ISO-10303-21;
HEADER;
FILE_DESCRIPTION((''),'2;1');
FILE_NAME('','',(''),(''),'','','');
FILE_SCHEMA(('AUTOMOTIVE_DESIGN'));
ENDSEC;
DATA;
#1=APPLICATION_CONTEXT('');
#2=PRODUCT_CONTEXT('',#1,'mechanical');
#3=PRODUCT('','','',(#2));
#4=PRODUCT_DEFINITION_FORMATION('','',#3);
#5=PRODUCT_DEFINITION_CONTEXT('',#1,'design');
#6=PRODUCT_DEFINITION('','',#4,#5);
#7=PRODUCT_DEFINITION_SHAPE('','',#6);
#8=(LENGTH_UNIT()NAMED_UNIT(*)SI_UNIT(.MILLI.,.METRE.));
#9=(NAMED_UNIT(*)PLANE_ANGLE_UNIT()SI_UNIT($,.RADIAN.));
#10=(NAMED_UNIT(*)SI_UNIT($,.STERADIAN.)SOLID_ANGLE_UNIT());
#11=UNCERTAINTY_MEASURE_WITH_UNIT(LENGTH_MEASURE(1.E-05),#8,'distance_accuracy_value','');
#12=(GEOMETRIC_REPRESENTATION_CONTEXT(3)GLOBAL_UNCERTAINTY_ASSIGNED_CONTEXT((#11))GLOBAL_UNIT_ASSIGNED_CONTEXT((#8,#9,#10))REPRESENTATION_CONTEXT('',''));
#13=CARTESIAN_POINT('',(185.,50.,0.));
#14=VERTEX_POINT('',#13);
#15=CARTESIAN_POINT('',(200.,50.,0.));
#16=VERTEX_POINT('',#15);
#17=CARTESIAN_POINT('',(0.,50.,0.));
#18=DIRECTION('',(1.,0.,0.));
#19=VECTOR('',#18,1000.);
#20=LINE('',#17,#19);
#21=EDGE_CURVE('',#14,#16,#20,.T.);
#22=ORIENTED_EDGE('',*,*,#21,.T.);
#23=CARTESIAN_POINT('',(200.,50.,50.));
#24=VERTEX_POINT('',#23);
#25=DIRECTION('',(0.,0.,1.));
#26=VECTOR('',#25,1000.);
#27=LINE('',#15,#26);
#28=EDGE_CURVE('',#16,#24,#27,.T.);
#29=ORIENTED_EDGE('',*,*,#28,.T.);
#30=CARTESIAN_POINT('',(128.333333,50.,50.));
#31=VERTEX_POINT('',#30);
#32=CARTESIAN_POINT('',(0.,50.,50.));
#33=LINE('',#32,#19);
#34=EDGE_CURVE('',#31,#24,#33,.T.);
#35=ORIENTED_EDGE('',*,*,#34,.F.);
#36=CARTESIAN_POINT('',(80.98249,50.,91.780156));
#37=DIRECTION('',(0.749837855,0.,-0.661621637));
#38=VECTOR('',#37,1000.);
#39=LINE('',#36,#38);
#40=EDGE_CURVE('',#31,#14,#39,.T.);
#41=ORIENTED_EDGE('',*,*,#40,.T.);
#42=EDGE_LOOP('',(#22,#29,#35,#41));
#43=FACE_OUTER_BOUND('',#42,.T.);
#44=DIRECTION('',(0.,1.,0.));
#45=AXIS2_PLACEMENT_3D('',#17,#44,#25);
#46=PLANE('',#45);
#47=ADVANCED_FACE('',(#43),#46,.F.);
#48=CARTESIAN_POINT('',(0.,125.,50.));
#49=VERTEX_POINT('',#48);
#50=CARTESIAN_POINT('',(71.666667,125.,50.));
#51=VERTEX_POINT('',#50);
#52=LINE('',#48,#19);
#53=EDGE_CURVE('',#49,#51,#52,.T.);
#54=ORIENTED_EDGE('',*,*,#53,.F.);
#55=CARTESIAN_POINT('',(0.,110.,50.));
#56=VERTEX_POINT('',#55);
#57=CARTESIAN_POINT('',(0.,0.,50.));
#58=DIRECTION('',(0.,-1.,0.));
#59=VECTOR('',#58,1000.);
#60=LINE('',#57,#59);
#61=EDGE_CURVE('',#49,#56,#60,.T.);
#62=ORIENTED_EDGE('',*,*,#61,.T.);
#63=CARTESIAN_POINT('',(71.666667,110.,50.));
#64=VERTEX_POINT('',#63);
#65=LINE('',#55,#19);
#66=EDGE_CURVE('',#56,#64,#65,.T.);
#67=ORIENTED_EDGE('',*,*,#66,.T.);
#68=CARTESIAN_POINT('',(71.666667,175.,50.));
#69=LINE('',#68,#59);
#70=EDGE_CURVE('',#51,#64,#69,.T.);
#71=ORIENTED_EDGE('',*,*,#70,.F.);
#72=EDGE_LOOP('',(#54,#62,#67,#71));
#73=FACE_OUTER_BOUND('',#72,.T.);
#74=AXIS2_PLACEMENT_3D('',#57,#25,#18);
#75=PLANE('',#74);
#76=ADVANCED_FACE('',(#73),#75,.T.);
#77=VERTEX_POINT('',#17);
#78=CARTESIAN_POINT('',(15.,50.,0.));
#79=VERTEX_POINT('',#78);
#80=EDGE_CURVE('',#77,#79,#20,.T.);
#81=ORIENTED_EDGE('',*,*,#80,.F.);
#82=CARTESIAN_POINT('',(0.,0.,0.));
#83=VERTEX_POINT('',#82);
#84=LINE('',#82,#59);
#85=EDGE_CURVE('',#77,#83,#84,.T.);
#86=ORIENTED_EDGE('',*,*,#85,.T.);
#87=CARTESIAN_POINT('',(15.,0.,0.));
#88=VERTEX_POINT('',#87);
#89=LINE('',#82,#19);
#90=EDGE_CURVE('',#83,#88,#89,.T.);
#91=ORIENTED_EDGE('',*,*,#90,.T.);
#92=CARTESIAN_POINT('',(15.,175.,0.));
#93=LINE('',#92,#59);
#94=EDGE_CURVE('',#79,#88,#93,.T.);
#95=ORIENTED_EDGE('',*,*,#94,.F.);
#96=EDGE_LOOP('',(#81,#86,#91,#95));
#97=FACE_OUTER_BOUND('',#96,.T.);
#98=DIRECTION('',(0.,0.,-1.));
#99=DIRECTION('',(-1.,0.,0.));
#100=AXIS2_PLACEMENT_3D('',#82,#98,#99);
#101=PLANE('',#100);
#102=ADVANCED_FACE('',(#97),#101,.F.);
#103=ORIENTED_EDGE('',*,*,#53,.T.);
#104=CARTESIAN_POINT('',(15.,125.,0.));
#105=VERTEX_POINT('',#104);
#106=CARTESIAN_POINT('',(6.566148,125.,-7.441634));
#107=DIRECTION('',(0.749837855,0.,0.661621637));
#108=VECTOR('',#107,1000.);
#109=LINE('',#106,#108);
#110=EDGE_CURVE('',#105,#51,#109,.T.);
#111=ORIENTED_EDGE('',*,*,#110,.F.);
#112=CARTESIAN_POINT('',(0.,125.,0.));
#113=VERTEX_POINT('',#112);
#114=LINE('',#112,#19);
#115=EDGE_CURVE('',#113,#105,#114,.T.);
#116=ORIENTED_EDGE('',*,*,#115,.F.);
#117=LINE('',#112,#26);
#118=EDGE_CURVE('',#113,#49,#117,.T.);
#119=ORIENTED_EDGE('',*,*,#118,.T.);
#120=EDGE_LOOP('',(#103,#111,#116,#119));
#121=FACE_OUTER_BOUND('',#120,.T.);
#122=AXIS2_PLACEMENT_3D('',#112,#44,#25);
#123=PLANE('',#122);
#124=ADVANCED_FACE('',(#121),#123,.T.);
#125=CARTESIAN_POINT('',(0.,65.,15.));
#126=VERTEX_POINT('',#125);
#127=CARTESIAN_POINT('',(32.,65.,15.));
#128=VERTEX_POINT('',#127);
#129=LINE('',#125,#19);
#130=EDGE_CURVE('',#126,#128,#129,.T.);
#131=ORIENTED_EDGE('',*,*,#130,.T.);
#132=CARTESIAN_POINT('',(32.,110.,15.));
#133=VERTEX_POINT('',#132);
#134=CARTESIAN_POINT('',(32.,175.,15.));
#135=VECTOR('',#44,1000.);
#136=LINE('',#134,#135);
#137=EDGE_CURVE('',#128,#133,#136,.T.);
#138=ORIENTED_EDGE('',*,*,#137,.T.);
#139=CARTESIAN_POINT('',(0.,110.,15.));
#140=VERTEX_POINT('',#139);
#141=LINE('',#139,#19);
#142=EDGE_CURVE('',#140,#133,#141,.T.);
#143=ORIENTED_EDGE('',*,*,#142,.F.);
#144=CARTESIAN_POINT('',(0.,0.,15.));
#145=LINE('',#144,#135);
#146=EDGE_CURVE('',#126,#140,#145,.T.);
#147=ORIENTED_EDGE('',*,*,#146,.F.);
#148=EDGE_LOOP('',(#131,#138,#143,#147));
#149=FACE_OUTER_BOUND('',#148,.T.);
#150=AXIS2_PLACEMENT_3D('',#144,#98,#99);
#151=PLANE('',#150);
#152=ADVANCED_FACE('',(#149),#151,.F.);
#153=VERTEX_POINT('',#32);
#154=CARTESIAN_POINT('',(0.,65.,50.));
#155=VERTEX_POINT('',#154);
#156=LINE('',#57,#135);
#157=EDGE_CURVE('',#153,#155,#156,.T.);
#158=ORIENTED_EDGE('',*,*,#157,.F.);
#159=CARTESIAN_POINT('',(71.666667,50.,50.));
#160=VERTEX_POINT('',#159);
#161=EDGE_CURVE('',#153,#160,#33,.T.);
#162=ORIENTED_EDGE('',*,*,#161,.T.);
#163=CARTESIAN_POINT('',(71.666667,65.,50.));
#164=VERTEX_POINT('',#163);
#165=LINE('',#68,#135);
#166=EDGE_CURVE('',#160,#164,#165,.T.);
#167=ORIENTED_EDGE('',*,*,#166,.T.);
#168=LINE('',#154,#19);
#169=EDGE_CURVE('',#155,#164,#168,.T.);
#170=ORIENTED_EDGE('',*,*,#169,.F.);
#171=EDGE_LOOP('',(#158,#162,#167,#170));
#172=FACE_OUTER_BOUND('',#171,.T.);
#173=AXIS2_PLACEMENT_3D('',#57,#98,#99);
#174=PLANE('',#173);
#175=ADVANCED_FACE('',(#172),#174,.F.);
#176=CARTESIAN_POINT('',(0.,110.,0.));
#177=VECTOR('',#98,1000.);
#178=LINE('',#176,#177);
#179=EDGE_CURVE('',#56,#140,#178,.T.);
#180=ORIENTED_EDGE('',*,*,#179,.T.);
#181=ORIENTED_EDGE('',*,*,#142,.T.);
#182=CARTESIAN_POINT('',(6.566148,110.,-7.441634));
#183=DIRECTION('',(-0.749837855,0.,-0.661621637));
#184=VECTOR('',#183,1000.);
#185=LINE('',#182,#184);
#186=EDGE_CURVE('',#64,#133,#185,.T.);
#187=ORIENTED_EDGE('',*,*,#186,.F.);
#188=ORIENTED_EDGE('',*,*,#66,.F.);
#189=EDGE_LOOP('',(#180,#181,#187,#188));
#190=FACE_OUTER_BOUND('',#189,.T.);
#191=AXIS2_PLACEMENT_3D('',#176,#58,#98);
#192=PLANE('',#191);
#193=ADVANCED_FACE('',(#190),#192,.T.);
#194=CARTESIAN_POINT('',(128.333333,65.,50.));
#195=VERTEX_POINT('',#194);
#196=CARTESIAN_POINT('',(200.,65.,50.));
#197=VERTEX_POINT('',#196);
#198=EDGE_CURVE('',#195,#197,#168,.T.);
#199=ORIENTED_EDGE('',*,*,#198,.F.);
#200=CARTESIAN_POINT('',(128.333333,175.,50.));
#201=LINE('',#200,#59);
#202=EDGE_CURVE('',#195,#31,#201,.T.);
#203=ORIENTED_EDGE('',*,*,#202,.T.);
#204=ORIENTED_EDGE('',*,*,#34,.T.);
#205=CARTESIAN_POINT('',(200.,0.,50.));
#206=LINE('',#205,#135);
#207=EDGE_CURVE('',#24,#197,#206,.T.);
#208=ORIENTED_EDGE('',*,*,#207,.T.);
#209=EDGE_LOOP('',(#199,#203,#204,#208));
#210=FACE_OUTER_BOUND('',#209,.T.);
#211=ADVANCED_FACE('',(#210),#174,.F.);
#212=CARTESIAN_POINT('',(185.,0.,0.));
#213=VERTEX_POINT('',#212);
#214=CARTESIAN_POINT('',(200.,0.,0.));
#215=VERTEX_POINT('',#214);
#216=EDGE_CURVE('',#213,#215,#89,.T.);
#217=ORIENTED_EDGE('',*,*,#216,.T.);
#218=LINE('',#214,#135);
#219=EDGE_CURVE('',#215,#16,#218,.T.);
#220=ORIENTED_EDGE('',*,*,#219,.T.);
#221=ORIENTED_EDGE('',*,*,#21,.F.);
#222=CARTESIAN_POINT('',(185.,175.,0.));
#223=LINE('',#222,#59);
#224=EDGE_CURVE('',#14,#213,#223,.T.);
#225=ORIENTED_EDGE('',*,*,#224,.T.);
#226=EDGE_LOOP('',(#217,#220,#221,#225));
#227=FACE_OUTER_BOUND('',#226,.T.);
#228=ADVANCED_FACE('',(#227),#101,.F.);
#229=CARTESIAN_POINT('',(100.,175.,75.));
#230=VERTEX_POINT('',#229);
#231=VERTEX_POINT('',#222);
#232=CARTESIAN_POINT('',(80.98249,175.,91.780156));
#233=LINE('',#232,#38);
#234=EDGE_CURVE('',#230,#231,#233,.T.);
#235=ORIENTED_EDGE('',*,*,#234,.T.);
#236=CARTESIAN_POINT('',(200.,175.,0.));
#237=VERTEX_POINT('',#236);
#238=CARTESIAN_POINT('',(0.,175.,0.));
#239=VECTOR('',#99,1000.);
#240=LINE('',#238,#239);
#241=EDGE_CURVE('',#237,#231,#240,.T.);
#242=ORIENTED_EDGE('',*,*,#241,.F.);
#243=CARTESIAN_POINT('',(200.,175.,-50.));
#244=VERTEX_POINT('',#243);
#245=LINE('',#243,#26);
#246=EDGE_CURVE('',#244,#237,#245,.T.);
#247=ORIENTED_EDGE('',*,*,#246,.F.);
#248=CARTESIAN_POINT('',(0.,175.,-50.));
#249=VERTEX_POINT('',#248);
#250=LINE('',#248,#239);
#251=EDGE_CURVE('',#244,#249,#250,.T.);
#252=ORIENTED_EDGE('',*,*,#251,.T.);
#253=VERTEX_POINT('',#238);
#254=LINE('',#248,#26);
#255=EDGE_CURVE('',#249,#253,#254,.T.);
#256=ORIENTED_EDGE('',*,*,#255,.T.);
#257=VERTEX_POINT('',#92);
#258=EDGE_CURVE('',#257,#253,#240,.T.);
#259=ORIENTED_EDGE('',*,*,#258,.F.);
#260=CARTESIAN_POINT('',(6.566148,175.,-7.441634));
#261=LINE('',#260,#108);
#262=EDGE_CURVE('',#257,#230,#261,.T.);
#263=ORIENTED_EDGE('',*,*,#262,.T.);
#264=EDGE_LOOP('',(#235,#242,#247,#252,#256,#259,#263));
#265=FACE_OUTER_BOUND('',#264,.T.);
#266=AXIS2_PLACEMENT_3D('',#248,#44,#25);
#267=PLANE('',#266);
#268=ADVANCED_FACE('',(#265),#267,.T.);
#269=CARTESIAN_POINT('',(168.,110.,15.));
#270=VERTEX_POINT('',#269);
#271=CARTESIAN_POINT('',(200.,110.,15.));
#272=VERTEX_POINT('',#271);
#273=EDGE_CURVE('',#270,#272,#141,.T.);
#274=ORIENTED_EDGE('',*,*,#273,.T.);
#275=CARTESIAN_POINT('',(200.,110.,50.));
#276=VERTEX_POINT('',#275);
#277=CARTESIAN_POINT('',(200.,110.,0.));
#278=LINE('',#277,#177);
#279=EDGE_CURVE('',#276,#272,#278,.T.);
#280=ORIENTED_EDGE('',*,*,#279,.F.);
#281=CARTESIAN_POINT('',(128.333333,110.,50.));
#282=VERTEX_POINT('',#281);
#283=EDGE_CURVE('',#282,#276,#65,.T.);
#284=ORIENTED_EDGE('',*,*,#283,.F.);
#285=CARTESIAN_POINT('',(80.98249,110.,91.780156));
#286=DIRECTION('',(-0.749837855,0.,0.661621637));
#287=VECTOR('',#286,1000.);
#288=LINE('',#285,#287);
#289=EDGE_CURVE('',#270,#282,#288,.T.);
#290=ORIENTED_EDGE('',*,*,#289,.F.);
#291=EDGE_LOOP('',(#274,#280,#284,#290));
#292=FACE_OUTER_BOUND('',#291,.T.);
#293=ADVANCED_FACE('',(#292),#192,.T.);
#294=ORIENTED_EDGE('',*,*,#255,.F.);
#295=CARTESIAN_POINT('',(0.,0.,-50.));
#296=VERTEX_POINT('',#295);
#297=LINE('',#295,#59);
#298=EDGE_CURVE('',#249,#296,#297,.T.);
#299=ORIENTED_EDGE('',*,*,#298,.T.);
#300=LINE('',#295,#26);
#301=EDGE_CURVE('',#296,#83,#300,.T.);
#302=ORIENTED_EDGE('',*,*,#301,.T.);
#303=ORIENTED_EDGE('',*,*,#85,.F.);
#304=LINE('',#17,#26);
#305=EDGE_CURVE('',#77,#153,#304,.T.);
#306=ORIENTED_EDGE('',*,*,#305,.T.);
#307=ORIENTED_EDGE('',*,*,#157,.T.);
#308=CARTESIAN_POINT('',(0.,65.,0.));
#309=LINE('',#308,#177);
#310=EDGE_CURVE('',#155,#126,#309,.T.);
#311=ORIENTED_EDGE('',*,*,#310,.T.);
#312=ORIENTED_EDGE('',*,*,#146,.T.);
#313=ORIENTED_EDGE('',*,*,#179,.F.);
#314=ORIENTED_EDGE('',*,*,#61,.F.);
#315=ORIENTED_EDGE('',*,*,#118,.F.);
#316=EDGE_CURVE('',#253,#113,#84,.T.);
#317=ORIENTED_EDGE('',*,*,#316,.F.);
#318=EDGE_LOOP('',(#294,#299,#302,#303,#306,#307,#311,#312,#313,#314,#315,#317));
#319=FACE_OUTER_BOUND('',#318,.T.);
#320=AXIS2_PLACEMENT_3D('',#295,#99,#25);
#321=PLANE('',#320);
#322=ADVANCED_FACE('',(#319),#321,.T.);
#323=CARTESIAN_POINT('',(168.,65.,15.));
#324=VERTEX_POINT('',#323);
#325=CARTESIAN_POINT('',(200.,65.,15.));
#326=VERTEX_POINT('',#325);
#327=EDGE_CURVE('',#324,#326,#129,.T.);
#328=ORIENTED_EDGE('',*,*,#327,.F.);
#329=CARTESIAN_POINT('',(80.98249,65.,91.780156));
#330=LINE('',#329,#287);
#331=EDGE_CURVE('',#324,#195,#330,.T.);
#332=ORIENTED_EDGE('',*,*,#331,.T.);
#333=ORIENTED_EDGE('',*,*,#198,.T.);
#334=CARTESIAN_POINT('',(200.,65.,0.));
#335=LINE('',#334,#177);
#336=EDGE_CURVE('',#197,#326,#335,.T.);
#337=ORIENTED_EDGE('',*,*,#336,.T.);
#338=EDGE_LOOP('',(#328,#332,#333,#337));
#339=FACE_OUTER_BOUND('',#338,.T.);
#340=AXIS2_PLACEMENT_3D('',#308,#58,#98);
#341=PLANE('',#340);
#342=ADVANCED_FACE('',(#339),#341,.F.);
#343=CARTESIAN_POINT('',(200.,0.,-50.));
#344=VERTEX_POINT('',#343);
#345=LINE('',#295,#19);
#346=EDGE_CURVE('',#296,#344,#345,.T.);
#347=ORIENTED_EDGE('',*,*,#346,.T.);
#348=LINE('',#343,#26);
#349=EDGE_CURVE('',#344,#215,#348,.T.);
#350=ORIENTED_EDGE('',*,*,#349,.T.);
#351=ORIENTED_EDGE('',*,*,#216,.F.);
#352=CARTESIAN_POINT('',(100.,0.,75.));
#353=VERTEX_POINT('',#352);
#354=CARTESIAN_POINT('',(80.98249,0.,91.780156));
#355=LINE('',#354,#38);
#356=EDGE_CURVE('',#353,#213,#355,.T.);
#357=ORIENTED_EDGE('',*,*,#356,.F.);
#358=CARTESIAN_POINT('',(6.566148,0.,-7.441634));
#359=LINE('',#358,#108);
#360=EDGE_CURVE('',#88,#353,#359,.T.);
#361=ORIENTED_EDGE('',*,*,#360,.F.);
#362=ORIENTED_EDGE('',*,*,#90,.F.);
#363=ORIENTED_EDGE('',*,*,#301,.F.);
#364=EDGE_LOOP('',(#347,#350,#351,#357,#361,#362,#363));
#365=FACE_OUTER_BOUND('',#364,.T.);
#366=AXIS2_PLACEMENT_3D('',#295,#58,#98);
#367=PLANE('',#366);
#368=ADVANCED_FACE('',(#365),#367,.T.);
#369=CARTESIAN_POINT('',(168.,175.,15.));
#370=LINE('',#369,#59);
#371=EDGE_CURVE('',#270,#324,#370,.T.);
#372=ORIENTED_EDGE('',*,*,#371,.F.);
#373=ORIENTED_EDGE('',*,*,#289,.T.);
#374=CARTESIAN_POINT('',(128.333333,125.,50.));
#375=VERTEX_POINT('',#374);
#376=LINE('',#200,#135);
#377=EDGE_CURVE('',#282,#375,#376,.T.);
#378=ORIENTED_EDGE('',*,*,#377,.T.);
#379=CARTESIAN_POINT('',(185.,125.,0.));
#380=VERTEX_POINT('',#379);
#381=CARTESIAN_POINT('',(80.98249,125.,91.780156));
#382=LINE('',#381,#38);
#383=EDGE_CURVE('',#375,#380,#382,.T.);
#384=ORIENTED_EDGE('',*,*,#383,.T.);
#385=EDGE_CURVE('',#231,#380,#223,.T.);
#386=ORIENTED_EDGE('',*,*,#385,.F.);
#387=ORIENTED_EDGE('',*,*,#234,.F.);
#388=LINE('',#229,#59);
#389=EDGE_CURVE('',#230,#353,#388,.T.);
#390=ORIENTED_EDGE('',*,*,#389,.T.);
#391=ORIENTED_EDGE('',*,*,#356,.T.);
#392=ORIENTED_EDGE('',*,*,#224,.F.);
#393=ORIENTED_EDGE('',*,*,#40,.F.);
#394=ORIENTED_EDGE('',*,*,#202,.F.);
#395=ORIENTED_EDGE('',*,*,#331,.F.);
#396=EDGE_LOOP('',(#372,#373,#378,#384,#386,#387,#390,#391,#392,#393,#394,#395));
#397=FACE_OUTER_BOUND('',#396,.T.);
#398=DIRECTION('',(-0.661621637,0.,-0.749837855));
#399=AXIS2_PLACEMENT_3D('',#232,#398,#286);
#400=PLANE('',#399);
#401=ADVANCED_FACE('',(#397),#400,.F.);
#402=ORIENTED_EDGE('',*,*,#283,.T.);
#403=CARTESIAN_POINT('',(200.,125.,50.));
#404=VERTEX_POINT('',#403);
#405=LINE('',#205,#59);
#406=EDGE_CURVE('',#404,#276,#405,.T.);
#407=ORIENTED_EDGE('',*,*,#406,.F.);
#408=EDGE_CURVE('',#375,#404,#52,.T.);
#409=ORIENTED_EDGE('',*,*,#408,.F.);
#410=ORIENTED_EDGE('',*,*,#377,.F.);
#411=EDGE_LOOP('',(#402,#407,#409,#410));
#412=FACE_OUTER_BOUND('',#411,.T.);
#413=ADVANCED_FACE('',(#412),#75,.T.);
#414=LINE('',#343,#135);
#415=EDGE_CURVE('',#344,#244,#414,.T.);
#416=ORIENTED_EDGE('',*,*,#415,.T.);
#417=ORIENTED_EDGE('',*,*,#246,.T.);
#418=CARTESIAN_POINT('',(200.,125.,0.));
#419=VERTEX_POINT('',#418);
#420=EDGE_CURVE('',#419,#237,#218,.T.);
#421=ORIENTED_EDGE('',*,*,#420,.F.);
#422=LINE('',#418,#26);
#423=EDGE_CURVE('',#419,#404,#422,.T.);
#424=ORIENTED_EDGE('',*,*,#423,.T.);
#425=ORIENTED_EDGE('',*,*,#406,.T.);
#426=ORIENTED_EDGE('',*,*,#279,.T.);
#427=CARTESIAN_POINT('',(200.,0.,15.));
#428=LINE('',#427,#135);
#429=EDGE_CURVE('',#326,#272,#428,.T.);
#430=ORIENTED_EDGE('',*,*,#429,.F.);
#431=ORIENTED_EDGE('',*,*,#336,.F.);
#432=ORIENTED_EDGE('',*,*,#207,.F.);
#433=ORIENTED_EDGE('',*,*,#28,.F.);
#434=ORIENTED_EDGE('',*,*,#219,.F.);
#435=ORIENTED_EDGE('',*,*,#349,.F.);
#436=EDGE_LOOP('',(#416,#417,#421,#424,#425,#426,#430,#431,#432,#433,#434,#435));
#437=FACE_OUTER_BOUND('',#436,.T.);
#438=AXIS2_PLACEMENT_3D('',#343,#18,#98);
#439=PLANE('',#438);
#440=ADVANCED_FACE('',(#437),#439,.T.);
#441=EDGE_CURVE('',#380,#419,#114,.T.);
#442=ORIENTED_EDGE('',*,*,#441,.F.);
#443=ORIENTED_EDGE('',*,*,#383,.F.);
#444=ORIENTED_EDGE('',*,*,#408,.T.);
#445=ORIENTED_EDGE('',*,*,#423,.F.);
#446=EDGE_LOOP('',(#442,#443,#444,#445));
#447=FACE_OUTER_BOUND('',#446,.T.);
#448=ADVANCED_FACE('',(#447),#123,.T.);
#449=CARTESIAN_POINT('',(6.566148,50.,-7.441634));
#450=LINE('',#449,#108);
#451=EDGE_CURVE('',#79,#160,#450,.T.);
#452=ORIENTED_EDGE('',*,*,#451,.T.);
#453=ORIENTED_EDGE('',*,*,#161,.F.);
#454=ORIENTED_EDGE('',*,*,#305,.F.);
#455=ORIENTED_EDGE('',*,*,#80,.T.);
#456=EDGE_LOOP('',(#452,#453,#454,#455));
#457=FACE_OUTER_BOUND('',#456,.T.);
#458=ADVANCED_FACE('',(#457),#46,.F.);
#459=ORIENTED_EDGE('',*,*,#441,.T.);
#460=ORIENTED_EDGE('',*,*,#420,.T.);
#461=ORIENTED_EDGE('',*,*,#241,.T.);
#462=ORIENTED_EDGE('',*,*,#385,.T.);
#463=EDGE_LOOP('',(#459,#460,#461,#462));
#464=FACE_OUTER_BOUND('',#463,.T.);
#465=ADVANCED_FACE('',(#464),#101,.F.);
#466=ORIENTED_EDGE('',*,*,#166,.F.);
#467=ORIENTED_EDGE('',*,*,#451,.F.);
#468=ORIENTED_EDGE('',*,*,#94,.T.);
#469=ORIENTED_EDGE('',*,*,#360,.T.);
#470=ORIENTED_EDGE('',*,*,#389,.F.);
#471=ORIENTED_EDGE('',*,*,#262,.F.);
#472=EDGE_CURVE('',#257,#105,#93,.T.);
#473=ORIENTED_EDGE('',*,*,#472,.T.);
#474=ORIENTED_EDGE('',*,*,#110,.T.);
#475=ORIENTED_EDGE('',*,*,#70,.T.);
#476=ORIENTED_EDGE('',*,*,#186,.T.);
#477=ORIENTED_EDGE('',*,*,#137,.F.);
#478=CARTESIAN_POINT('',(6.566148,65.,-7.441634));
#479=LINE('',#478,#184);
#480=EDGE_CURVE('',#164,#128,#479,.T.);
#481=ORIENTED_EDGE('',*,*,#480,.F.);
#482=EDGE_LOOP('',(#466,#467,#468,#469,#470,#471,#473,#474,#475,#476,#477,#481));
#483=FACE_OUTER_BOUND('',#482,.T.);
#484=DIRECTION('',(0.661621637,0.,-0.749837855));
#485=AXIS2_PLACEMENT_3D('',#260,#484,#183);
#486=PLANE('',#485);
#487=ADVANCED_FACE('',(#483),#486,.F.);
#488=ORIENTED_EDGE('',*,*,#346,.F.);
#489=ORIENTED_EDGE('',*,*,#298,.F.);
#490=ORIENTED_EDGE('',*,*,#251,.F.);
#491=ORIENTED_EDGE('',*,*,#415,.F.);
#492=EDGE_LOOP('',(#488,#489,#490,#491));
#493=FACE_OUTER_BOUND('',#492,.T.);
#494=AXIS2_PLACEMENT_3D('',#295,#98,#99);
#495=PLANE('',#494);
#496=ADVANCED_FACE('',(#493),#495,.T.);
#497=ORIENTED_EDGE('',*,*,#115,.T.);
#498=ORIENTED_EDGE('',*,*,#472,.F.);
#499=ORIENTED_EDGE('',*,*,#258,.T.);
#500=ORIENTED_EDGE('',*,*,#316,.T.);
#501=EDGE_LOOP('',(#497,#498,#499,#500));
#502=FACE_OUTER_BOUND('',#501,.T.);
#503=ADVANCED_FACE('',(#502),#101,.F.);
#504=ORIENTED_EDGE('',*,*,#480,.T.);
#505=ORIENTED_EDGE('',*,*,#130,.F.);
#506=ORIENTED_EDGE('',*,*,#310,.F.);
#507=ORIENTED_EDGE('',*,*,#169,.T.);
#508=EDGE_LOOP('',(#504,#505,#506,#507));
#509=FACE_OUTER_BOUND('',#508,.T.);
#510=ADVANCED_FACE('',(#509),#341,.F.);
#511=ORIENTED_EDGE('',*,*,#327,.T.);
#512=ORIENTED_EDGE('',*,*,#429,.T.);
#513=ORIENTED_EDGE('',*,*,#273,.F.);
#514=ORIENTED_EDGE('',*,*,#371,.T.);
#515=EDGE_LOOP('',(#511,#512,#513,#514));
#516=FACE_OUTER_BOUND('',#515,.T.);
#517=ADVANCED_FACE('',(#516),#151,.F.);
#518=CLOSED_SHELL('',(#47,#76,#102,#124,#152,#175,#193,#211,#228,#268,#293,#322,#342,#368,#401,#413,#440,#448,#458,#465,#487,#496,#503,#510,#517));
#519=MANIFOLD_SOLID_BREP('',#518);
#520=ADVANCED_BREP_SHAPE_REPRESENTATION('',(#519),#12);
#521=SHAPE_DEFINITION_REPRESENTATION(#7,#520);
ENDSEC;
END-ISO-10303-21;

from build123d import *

# Parameters (mm, degrees)
BASE_BLOCK_PROFILE_W   = 200
BASE_BLOCK_PROFILE_H   = 175
BASE_BLOCK_DEPTH       = 50
NOTCHED_BOSS_175_DEPTH = 175
NOTCHED_BOSS_200_DEPTH = 200


with BuildPart() as part:
    # Base Block Profile → Base Block (new body)
    with BuildSketch(Plane.XY):
        with Locations((100, 87.5)):
            Rectangle(BASE_BLOCK_PROFILE_W, BASE_BLOCK_PROFILE_H)
    extrude(amount=-BASE_BLOCK_DEPTH)

    # Notched Boss Profile 175 → Notched Boss 175 (add)
    with BuildSketch(Plane.XZ):
        Polygon((100, 75), (15, 0), (185, 0), align=None)
    extrude(amount=-NOTCHED_BOSS_175_DEPTH)

    # Notched Boss Profile 200 → Notched Boss 200 (add)
    with BuildSketch(Plane(origin=(200, 0, 0), x_dir=(0, 0, -1), z_dir=(1, 0, 0))):
        Polygon((0, 50), (0, 125), (-50, 125), (-50, 110), (-15, 110), (-15, 65), (-50, 65), (-50, 50), (-15, 50), align=None)
    extrude(amount=-NOTCHED_BOSS_200_DEPTH)


solid = part.part
